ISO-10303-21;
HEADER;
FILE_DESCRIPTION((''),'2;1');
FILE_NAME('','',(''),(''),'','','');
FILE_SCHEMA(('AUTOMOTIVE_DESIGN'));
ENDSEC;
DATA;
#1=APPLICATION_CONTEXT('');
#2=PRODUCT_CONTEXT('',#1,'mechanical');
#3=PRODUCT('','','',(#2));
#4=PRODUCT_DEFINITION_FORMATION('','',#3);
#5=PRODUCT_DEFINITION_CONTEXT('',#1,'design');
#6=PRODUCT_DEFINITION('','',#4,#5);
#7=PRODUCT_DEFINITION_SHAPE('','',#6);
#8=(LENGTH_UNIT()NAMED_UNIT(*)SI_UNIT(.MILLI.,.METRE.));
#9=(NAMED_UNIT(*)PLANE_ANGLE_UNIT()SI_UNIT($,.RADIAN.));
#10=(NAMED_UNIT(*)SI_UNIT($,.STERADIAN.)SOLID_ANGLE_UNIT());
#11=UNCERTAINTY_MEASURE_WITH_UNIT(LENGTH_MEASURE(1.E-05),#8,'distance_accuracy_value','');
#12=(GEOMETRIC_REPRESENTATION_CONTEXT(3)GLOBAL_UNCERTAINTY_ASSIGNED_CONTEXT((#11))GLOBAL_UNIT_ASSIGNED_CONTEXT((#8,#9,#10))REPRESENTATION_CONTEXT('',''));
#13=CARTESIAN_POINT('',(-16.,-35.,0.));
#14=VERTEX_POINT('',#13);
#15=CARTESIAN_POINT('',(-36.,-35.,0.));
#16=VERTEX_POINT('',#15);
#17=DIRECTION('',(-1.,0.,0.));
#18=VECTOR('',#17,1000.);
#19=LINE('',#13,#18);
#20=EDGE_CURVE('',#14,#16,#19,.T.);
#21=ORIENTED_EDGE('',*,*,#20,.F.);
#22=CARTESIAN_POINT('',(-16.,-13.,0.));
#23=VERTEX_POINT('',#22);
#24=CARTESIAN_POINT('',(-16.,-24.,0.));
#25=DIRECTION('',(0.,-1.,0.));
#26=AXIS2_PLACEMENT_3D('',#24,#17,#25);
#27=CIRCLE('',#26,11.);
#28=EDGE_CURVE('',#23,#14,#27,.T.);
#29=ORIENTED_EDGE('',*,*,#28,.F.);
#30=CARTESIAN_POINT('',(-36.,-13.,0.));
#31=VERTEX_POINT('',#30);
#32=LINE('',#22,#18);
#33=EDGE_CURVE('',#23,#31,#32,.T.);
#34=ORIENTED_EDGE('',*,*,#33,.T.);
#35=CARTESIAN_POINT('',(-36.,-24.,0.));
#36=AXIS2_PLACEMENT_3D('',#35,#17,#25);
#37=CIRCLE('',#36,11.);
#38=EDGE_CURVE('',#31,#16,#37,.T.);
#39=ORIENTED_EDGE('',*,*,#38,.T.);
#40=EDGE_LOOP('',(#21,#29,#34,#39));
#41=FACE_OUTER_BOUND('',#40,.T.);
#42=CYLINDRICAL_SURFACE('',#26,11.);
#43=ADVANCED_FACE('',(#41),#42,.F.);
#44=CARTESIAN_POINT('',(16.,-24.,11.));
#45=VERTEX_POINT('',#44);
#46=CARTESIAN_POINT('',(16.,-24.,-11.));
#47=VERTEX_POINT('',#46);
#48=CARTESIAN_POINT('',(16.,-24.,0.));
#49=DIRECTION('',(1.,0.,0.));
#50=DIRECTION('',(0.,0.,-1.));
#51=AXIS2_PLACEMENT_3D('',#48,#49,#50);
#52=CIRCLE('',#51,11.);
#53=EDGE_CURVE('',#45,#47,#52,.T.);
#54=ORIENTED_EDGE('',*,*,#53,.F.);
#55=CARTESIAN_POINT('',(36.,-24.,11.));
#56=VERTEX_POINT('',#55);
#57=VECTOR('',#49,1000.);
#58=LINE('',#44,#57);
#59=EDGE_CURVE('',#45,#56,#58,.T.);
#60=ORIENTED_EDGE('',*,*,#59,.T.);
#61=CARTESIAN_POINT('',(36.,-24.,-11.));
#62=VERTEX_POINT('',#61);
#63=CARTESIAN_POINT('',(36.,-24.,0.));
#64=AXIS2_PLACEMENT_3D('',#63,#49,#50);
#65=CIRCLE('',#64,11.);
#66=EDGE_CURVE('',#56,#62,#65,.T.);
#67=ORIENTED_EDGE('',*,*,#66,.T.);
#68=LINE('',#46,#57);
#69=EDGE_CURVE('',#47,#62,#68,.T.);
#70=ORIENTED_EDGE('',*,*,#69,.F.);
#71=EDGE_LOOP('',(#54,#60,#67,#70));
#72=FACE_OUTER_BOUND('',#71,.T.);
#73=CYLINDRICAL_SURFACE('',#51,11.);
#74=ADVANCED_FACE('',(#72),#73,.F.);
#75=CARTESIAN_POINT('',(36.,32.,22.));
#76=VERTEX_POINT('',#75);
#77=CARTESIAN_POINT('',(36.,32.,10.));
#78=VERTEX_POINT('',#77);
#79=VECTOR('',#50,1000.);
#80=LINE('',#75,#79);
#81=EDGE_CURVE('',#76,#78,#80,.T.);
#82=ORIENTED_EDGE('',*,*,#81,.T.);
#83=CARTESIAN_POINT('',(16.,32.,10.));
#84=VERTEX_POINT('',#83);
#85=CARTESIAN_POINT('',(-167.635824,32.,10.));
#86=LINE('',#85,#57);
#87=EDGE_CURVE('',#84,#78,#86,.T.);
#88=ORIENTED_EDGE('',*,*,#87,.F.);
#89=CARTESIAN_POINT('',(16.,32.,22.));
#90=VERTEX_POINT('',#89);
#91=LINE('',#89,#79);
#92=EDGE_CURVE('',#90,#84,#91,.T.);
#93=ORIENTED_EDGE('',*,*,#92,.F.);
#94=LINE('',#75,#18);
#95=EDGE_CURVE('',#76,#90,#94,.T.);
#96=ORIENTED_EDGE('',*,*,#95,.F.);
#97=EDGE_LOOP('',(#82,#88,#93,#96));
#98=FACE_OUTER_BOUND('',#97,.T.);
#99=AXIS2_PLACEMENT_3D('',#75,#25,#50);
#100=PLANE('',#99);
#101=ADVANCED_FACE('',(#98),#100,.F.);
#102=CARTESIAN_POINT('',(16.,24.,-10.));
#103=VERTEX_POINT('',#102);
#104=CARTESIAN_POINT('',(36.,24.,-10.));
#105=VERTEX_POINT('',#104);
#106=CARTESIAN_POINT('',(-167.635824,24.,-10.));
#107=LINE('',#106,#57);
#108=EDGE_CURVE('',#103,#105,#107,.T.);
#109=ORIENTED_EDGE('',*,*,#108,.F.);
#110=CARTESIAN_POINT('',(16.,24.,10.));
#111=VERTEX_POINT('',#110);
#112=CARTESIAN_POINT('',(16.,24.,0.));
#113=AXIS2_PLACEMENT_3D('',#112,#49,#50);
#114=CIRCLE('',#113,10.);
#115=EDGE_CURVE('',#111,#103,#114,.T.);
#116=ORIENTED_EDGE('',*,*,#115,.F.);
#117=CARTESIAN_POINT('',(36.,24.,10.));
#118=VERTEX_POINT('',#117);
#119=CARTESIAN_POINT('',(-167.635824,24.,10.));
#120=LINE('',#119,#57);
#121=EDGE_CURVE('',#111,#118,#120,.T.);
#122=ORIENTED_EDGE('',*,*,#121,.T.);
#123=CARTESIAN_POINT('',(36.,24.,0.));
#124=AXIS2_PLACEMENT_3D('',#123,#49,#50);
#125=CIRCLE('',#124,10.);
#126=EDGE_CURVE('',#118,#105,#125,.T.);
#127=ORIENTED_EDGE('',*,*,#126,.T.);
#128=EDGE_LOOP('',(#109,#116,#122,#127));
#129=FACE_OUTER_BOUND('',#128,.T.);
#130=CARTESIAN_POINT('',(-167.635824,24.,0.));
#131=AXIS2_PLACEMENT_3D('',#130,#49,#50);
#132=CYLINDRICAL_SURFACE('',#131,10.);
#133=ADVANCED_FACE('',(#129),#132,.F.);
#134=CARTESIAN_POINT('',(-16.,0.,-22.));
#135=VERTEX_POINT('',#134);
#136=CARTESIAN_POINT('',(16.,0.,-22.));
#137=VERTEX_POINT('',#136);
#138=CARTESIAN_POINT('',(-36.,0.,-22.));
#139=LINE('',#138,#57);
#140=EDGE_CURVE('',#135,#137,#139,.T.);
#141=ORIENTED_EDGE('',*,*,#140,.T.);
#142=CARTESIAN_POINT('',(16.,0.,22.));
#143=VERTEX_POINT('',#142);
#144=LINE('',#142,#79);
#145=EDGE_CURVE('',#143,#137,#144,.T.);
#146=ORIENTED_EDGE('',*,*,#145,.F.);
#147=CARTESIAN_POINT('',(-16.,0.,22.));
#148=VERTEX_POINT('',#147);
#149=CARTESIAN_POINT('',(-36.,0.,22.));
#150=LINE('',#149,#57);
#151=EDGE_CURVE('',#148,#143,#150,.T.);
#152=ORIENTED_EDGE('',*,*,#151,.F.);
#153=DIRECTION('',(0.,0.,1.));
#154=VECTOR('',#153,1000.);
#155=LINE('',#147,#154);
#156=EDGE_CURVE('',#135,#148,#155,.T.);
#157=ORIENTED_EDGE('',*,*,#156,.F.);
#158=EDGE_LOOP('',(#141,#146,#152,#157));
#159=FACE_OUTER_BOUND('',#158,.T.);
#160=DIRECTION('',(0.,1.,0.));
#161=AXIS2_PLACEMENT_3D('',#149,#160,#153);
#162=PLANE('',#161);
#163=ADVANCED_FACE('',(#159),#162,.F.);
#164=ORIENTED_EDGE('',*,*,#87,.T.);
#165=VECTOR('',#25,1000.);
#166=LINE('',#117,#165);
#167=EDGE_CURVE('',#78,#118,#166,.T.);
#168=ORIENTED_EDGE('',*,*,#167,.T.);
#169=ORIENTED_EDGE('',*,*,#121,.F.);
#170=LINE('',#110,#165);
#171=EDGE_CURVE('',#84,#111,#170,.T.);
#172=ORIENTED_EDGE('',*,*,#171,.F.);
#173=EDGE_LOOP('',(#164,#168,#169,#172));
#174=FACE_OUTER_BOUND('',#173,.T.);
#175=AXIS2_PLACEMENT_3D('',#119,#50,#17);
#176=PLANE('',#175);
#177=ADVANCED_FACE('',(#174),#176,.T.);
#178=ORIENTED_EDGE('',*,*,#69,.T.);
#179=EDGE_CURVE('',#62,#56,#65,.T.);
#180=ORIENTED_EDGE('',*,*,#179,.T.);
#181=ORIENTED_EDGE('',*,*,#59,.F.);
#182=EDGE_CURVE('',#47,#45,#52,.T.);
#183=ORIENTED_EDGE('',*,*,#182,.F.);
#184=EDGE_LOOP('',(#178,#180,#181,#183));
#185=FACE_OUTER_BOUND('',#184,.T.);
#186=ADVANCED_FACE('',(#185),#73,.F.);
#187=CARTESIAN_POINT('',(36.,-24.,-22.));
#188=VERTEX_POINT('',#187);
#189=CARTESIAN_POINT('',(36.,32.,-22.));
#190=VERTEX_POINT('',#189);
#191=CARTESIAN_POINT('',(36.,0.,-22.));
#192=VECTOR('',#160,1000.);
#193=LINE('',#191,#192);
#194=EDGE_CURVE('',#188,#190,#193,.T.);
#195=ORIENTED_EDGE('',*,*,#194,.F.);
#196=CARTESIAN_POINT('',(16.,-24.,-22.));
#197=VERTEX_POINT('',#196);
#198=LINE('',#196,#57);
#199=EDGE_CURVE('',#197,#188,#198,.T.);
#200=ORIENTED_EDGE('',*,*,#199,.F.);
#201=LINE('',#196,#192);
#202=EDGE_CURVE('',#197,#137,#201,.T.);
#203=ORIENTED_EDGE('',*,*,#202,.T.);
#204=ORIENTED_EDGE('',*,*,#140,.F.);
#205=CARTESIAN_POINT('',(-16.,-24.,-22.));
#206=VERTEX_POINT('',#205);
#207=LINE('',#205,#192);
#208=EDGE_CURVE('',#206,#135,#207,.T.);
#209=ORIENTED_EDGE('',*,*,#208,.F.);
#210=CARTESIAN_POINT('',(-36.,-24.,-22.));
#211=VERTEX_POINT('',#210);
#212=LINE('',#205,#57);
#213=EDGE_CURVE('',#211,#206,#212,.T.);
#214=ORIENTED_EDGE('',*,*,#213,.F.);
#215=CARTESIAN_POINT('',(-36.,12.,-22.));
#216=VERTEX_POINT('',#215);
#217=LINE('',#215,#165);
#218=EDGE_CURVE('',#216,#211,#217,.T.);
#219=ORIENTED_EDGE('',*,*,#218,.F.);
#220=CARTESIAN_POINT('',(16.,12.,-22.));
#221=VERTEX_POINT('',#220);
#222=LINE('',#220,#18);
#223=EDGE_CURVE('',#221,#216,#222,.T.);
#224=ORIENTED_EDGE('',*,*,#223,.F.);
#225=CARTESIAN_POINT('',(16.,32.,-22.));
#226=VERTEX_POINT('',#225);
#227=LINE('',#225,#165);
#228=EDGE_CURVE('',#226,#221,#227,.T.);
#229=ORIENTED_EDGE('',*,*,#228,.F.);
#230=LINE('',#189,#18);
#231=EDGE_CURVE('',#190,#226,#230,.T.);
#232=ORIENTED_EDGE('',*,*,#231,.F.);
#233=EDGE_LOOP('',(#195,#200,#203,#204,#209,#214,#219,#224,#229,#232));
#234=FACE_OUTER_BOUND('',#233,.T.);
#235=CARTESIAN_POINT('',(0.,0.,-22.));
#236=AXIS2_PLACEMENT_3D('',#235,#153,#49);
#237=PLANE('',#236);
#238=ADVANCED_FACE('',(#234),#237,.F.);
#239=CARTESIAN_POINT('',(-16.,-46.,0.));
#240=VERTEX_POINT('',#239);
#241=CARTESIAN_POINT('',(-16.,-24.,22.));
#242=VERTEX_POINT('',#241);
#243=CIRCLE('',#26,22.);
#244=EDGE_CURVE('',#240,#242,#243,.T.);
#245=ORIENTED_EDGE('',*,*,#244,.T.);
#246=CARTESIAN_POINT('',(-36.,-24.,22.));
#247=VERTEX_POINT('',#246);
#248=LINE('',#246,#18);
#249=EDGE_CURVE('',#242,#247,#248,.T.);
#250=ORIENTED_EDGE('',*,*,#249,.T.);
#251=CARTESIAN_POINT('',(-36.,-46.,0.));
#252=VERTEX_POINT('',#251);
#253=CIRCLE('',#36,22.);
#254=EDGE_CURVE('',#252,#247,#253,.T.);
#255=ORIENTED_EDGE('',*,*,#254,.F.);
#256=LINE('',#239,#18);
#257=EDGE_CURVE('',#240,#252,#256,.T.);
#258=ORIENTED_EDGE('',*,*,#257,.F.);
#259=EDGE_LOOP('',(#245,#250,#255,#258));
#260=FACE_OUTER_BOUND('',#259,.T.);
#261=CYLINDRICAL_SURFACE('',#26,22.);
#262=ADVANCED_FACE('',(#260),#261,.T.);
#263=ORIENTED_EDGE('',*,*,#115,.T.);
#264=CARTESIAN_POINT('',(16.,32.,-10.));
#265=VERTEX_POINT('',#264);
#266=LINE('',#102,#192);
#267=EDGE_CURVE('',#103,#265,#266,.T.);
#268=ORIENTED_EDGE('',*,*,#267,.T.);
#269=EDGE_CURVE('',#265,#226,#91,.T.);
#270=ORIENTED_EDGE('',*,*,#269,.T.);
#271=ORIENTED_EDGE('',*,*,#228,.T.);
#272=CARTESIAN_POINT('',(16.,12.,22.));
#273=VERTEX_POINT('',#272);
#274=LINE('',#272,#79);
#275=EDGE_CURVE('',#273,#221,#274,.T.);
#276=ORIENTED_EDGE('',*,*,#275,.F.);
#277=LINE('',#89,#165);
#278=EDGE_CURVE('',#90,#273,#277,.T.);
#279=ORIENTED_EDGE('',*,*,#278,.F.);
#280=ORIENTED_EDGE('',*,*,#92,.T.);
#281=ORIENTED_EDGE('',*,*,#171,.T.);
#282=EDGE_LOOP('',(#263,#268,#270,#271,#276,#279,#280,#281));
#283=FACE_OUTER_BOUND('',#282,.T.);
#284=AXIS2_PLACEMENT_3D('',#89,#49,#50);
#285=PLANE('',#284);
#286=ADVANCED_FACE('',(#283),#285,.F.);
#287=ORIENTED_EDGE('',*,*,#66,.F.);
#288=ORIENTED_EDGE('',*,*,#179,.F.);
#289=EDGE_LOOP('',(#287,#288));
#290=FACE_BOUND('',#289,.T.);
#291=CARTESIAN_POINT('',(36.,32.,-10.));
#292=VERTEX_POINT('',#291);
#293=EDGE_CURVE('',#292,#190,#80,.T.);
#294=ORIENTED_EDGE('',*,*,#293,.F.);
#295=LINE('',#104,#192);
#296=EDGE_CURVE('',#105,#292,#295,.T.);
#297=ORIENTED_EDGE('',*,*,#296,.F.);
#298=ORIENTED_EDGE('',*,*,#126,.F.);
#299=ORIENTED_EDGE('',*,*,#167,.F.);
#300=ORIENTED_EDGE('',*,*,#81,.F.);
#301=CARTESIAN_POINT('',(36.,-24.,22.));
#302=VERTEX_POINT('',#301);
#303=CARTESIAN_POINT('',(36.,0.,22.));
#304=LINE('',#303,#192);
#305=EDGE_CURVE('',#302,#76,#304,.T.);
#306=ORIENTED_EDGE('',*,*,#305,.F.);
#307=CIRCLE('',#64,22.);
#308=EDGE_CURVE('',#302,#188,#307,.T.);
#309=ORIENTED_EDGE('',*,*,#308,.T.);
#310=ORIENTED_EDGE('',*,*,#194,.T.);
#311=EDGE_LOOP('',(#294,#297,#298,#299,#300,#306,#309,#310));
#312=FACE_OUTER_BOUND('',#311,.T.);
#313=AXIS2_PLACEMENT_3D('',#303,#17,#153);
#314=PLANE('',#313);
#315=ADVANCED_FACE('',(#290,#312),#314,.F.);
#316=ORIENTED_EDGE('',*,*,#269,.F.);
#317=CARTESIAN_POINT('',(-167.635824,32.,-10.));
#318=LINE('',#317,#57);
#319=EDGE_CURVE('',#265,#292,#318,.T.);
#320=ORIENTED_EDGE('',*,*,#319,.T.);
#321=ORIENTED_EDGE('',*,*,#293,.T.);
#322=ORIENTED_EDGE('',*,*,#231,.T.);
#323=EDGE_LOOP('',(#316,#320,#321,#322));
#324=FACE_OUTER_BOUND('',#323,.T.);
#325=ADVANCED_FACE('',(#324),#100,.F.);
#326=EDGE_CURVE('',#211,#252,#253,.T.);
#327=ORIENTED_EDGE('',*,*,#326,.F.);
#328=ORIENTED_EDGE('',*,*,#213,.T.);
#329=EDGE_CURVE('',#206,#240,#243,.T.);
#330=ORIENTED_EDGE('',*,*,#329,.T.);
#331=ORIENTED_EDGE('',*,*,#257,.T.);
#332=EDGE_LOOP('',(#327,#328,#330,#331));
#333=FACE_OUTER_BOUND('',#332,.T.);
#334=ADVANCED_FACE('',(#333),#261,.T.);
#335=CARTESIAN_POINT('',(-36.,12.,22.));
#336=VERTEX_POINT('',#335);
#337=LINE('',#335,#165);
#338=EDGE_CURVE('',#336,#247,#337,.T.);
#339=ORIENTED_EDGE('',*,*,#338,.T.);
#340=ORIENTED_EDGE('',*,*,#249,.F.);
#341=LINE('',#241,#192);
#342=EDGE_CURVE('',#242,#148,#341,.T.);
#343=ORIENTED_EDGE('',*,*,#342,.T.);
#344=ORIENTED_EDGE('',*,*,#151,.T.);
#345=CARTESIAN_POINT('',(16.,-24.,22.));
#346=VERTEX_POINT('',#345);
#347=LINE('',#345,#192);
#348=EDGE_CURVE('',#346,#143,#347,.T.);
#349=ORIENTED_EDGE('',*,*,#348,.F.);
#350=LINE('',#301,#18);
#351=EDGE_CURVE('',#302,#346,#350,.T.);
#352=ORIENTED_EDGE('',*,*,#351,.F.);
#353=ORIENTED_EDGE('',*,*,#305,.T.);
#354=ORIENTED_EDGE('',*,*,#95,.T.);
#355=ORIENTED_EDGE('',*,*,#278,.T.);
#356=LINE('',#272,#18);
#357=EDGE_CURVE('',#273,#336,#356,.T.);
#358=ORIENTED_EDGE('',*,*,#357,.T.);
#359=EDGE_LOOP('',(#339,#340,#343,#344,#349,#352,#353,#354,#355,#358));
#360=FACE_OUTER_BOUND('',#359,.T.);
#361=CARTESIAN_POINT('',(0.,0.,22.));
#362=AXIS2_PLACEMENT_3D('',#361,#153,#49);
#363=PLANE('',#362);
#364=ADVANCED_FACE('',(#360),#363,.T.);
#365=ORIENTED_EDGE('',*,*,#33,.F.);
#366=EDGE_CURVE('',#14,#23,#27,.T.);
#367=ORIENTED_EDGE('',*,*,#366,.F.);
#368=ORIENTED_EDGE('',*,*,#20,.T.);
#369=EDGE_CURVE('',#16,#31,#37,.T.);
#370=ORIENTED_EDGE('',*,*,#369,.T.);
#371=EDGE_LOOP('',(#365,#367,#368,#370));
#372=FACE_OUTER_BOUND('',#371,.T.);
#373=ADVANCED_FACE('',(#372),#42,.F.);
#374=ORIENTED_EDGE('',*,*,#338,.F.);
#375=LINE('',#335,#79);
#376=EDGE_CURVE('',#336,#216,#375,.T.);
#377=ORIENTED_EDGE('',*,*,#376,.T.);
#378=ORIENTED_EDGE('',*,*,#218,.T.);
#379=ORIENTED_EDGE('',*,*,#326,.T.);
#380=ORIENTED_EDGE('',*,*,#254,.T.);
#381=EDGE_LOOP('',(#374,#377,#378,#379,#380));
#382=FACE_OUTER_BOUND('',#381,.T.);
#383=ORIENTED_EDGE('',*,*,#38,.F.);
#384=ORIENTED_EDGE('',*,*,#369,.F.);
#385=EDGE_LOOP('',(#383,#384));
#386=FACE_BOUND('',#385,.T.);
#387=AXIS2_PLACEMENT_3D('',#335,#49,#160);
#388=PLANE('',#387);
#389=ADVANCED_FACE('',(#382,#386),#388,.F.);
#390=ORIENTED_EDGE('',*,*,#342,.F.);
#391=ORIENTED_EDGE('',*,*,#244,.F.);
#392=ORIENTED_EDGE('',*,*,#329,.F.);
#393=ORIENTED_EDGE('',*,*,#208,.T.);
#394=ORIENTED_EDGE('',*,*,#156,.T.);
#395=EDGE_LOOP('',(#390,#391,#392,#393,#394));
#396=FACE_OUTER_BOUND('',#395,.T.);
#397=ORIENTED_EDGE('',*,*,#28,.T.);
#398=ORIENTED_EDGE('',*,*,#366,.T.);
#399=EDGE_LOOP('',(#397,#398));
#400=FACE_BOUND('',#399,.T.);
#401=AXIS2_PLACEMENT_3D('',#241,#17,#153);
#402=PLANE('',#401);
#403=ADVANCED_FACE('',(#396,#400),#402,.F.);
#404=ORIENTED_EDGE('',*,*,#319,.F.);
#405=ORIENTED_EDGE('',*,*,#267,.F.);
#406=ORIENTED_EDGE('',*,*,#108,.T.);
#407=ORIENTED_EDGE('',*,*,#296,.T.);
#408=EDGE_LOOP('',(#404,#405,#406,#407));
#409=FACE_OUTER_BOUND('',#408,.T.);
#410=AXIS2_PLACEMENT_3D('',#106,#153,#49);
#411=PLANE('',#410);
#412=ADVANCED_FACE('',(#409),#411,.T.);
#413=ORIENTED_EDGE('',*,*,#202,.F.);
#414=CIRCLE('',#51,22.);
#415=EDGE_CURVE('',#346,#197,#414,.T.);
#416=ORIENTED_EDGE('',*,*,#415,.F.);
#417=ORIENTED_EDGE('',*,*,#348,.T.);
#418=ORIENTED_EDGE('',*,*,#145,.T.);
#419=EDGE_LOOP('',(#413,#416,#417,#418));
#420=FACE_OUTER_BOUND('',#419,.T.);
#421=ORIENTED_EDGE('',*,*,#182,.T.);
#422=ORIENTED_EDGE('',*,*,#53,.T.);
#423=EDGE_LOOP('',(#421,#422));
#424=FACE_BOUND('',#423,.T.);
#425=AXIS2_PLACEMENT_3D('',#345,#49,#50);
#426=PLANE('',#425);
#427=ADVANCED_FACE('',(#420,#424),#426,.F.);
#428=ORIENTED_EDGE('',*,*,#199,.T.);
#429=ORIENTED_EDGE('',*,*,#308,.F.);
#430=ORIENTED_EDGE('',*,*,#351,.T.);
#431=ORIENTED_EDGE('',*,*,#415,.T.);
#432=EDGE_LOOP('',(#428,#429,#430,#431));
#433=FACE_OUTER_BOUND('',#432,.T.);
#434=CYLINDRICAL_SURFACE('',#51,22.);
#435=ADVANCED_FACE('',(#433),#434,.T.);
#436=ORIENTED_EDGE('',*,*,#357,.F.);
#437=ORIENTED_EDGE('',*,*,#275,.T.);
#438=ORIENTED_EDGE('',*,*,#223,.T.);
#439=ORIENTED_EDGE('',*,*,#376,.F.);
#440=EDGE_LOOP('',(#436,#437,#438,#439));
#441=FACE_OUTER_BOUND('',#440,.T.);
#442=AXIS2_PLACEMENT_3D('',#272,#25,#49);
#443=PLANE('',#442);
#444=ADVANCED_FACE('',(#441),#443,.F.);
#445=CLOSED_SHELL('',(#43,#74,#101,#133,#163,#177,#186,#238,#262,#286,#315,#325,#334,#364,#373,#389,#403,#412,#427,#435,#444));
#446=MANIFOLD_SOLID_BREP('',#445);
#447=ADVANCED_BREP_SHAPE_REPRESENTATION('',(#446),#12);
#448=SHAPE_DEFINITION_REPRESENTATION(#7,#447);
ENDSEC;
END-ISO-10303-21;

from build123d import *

# Parameters (mm, degrees)
BASE_BLOCK_DEPTH       = 22
LUG_WEB_SKETCH_W       = 20
LUG_WEB_SKETCH_H       = 44
LUG_WEB_DEPTH          = 24
LUG_BOSS_1_SKETCH_R    = 22
LUG_BOSS_1_SKETCH_R_2  = 11
LUG_BOSS_1_R22_DEPTH   = 20
LUG_HOLE_1_SKETCH_R    = 11
LUG_HOLE_1_DEPTH       = 20
LUG_START              = -20
LUG_BOSS_2_SKETCH_R    = 22
LUG_BOSS_2_SKETCH_R_2  = 11
LUG_BOSS_2_R22_DEPTH   = 20
LUG_HOLE_2_SKETCH_R    = 11
LUG_HOLE_2_DEPTH       = 20
CLEVIS_SLOT_DEPTH      = 73.828565824
CLEVIS_SLOT_DEPTH_BACK = 20


with BuildPart() as part:
    # Base Profile Sketch → Base Block (new, symmetric)
    with BuildSketch(Plane.XY):
        Polygon((-36, 0), (36, 0), (36, 32), (16, 32), (16, 12), (-36, 12), align=None)
    extrude(amount=BASE_BLOCK_DEPTH, both=True)

    # Lug Web Sketch → Lug Web (add)
    with BuildSketch(Plane.XZ):
        with Locations((-26, 0)):
            Rectangle(LUG_WEB_SKETCH_W, LUG_WEB_SKETCH_H)
        with Locations((26, 0)):
            Rectangle(LUG_WEB_SKETCH_W, LUG_WEB_SKETCH_H)
    extrude(amount=LUG_WEB_DEPTH)

    # Lug Boss 1 Sketch → Lug Boss 1 R22 (add)
    with BuildSketch(Plane.ZY.offset(36)):
        with Locations((0, -24)):
            Circle(LUG_BOSS_1_SKETCH_R)
        with Locations((0, -24)):
            Circle(LUG_BOSS_1_SKETCH_R_2, mode=Mode.SUBTRACT)
    extrude(amount=-LUG_BOSS_1_R22_DEPTH)

    # Lug Hole 1 Sketch → Lug Hole 1 (cut)
    with BuildSketch(Plane.ZY.offset(36)):
        with Locations(Location((0, -24, 0), (0, 0, 270))):
            Circle(LUG_HOLE_1_SKETCH_R)
    extrude(amount=-LUG_HOLE_1_DEPTH, mode=Mode.SUBTRACT)

    # Lug Boss 2 Sketch → Lug Boss 2 R22 (add)
    with BuildSketch(Plane(origin=(36, 0, 0), x_dir=(0, 0, -1), z_dir=(1, 0, 0)).offset(LUG_START)):
        with Locations((0, -24)):
            Circle(LUG_BOSS_2_SKETCH_R)
        with Locations(Location((0, -24, 0), (0, 0, 270))):
            Circle(LUG_BOSS_2_SKETCH_R_2, mode=Mode.SUBTRACT)
    extrude(amount=LUG_BOSS_2_R22_DEPTH)

    # Lug Hole 2 Sketch → Lug Hole 2 (cut)
    with BuildSketch(Plane(origin=(36, 0, 0), x_dir=(0, 0, -1), z_dir=(1, 0, 0)).offset(LUG_START)):
        with Locations(Location((0, -24, 0), (0, 0, 270))):
            Circle(LUG_HOLE_2_SKETCH_R)
    extrude(amount=LUG_HOLE_2_DEPTH, mode=Mode.SUBTRACT)

    # Clevis Slot Sketch → Clevis Slot (cut, two sides: drawn at the far end of the back side and taken through both)
    with BuildSketch(Plane.ZY.offset(-16).offset(-CLEVIS_SLOT_DEPTH_BACK)):
        with BuildLine():
            Line((-10, 32), (-10, 24))
            ThreePointArc((-10, 24), (0, 14), (10, 24))
            Line((10, 24), (10, 32))
            Line((10, 32), (-10, 32))
        make_face()
    extrude(amount=CLEVIS_SLOT_DEPTH + CLEVIS_SLOT_DEPTH_BACK, mode=Mode.SUBTRACT)


solid = part.part
